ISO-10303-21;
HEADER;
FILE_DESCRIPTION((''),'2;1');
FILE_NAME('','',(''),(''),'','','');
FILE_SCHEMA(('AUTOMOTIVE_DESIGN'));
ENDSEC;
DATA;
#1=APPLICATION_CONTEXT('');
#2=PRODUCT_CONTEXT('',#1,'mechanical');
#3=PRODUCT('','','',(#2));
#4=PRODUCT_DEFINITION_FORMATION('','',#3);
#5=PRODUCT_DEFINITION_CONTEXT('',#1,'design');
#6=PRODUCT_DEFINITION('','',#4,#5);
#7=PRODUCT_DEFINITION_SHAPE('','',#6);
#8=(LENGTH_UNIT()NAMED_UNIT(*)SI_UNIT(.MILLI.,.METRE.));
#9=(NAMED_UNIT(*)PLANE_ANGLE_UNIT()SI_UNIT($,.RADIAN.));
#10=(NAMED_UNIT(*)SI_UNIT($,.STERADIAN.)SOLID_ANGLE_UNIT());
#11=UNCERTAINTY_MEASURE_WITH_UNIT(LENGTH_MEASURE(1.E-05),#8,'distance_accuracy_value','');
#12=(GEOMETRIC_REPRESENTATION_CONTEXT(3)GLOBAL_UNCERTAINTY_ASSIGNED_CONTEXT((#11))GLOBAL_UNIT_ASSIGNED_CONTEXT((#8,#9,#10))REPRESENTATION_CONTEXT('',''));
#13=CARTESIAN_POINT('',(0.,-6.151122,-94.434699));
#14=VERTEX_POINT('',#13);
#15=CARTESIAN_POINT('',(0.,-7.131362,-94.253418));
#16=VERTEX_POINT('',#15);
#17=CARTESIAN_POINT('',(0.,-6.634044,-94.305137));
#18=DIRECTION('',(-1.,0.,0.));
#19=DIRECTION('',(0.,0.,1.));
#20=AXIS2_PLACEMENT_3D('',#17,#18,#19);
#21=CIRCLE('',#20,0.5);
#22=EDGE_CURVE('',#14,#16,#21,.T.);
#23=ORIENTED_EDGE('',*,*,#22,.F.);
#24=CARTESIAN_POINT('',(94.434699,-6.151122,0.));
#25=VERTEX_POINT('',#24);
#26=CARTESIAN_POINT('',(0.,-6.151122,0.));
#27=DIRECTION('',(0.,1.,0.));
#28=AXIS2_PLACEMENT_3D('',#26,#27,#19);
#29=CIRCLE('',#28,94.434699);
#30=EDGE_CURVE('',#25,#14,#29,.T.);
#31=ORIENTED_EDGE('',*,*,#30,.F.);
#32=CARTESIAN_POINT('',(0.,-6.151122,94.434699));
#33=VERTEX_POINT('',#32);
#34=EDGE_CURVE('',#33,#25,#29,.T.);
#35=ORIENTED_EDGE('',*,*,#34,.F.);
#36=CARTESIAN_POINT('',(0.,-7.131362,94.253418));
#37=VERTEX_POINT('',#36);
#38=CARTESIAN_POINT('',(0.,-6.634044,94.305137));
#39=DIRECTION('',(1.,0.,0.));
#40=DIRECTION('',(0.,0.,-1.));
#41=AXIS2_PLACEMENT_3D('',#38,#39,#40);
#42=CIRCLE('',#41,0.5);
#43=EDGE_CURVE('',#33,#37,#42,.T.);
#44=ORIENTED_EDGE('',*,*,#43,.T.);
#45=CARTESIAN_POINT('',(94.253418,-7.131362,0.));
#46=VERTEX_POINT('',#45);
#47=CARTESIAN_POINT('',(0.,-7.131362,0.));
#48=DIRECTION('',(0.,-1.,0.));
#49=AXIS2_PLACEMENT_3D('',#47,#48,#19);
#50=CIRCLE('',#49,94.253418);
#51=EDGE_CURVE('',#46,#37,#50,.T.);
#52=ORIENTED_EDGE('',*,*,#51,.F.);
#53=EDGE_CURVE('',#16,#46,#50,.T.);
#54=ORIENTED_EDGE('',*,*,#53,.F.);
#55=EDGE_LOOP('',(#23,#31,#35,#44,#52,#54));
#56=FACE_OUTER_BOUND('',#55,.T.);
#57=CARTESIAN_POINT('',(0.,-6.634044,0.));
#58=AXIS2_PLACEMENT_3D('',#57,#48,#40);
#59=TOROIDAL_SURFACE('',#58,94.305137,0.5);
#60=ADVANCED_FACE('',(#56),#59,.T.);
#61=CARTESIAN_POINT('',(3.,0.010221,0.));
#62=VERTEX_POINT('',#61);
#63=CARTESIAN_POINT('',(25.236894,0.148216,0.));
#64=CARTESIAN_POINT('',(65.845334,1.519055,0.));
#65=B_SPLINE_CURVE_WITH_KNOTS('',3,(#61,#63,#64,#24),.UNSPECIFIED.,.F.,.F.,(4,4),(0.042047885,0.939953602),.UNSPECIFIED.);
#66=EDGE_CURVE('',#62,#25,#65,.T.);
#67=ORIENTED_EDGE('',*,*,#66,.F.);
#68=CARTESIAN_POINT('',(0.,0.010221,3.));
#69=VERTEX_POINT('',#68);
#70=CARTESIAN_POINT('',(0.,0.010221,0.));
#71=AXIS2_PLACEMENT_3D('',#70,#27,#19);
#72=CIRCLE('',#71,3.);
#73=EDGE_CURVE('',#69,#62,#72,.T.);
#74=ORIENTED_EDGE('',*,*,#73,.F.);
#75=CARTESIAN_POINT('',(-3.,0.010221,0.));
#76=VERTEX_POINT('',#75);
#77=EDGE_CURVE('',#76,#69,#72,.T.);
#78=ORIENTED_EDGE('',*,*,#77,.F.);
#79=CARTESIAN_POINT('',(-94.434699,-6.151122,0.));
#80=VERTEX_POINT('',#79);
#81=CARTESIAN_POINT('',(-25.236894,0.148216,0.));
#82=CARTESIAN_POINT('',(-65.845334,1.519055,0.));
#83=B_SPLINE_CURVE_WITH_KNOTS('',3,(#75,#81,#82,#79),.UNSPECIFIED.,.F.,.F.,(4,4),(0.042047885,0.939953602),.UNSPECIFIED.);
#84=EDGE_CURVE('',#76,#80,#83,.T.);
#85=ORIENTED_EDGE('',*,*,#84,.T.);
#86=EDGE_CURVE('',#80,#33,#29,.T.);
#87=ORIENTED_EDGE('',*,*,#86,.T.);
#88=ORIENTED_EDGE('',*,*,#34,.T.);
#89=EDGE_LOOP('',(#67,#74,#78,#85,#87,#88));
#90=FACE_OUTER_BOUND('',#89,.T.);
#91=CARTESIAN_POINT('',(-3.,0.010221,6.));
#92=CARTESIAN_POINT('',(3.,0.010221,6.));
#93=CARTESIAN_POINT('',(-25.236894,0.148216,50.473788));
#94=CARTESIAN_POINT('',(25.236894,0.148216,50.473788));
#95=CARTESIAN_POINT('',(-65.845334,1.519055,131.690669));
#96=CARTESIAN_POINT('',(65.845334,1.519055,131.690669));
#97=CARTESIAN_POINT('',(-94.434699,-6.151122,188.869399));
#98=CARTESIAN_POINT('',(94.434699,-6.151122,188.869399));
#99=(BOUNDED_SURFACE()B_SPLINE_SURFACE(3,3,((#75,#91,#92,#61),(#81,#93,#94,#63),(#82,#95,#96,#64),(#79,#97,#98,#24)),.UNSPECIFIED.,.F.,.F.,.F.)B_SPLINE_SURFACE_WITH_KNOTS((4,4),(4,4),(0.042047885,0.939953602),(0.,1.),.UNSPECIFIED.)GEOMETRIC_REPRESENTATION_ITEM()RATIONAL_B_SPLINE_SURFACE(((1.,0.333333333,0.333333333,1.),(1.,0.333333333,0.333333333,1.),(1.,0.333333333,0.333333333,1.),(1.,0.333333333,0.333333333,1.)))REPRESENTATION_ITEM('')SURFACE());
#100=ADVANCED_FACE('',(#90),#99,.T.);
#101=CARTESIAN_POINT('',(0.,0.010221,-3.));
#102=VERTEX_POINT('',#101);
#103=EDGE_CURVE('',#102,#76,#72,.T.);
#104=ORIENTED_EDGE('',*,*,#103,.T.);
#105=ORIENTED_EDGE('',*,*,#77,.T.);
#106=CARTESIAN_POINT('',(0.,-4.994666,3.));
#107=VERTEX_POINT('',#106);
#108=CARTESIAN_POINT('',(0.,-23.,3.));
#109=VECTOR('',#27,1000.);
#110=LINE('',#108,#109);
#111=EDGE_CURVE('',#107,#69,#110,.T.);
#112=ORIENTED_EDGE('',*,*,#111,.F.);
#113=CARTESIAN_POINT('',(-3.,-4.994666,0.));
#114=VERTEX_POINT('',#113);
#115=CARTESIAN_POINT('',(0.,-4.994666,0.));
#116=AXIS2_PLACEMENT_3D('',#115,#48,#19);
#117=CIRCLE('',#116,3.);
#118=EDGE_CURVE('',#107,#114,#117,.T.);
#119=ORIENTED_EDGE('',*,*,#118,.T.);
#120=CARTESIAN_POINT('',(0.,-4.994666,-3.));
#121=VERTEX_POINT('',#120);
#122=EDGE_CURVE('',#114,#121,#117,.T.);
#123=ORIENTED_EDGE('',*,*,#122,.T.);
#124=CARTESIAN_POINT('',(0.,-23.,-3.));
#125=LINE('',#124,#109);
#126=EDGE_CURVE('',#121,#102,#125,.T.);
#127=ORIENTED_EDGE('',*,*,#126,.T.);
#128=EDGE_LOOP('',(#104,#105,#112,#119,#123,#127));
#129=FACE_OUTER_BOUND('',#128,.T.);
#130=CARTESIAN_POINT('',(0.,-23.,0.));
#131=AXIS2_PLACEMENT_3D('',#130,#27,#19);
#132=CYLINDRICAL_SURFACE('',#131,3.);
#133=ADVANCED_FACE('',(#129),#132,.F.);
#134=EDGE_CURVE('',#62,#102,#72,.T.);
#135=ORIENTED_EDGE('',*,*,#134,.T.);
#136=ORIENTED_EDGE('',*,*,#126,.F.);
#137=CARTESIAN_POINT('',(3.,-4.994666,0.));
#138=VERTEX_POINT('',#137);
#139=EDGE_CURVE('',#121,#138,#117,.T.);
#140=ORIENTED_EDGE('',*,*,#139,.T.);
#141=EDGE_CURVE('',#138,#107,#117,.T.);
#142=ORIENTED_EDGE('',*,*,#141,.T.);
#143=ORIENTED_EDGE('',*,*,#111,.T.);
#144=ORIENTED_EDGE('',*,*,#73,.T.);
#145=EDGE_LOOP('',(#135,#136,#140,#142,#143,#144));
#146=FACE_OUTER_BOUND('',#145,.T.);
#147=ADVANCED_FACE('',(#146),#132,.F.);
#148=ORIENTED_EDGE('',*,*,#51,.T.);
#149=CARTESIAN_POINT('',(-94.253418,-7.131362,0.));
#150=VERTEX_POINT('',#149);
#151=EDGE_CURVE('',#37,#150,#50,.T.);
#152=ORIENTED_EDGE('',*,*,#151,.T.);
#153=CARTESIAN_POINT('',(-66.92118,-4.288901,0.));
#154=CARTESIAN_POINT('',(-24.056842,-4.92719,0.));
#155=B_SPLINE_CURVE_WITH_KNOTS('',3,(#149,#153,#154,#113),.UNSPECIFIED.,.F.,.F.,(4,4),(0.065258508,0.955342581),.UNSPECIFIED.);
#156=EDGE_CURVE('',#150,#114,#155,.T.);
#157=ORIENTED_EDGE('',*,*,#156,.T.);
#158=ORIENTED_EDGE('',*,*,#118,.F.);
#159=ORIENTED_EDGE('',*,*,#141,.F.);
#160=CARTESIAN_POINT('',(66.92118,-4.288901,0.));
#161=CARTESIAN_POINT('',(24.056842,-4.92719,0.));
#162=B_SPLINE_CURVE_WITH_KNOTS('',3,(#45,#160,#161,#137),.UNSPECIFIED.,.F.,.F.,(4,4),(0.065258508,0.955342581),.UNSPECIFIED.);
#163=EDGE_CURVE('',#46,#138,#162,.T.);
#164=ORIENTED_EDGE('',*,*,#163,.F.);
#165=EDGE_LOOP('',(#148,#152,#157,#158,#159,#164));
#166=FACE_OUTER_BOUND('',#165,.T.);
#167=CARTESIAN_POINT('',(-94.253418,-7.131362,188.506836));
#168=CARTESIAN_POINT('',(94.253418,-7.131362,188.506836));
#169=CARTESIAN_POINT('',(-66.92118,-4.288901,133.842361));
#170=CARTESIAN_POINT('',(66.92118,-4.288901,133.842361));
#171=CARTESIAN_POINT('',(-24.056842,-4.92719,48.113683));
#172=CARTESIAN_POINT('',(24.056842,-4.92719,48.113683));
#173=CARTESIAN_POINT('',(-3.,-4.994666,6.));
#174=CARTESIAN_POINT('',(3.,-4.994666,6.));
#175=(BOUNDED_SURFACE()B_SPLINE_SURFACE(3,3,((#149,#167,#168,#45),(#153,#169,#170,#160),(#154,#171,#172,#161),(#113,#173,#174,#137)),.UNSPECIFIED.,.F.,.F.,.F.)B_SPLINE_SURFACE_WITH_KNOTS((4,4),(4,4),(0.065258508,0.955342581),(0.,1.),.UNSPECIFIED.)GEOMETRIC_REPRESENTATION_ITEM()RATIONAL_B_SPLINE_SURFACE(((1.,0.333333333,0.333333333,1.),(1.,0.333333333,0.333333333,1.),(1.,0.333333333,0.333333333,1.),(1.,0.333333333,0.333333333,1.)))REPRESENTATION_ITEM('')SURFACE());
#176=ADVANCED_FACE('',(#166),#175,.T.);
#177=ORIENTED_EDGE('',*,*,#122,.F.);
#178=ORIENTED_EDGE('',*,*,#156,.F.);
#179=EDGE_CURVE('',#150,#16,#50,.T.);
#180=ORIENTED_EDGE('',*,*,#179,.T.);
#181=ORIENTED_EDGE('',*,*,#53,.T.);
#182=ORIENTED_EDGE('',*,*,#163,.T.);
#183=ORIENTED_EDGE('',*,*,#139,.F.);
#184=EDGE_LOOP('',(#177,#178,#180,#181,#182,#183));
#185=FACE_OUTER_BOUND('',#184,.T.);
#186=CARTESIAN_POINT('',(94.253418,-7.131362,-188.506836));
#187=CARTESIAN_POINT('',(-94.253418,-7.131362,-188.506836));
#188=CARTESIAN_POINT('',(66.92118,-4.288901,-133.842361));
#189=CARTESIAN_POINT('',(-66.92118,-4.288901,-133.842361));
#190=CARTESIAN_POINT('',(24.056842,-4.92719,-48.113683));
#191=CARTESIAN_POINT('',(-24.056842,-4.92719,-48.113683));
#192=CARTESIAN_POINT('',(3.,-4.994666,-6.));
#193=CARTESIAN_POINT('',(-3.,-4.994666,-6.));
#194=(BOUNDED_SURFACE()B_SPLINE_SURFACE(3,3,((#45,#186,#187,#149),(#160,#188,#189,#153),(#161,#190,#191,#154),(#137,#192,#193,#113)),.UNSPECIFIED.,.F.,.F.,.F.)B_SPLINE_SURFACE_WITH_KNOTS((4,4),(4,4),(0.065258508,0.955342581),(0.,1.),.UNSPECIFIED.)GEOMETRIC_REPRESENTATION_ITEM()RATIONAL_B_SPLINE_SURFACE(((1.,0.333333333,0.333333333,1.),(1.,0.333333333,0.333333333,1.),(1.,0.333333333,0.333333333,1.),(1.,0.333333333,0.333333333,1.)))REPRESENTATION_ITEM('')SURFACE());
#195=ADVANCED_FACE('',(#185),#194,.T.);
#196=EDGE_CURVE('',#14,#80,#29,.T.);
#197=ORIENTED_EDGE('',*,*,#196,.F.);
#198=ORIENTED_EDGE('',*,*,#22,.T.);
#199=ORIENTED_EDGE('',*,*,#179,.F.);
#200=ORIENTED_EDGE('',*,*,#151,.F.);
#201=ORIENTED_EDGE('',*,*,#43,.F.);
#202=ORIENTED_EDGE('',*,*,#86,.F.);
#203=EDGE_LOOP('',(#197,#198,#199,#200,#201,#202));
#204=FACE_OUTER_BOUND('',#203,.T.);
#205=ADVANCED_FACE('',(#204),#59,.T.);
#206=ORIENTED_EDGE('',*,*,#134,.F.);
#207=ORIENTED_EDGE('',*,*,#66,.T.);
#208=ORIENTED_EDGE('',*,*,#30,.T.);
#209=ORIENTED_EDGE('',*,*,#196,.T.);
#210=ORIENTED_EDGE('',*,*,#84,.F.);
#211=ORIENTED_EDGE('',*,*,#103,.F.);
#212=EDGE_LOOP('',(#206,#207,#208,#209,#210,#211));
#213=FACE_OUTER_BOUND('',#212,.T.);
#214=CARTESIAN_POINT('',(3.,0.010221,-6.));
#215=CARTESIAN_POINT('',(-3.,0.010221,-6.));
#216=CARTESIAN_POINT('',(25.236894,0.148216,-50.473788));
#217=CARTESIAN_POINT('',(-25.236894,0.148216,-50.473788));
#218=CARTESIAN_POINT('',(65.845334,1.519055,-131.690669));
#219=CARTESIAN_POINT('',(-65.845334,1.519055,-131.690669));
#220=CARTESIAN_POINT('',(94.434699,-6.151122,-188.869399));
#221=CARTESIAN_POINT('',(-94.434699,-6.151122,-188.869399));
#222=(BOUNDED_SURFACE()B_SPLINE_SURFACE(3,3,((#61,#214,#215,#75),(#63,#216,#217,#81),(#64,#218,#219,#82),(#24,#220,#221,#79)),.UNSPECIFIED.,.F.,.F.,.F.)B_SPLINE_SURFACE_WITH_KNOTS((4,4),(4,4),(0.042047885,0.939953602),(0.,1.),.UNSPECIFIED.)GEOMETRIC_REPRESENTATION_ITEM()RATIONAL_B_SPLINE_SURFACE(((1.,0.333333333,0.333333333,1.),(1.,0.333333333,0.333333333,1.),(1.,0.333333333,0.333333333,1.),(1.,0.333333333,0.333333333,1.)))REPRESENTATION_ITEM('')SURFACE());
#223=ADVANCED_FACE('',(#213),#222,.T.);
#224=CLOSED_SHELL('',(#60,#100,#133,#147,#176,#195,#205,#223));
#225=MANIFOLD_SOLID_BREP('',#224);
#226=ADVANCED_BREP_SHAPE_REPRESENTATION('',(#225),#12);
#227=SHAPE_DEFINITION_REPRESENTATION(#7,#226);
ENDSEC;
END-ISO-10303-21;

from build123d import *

# Parameters (mm, degrees)
FILLET_1_R          = 0.5
SKETCH_2_R          = 3
CUT_EXTRUDE_1_DEPTH = 23


with BuildPart() as part:
    # 草图1 → 旋转1 (revolve)
    with BuildSketch(Plane.XY):
        with BuildLine():
            Line((0, 0), (0, -5))
            add(Edge.make_bspline(
                [(-100, -7.814294025), (-72.076817605, -4.022924744), (-21.093053963, -5), (0, -5)],
                knots=[0, 0, 0, 0, 1, 1, 1, 1], degree=3))
            add(Edge.make_bspline(
                [(-100, -7.814294025), (-70.101614167, 2.125878409), (-22.774788705, 0), (0, 0)],
                knots=[0, 0, 0, 0, 1, 1, 1, 1], degree=3))
        make_face()
    revolve(axis=Axis((0, 0, 0), (0, -1, 0)))

    # 圆角1
    fillet_1_edges = [part.edges().sort_by_distance(p)[0] for p in [
        (100, -7.814294025, 0),
    ]]
    fillet(fillet_1_edges, radius=FILLET_1_R)

    # 草图2 → 切除-拉伸1 (cut, symmetric)
    with BuildSketch(Plane(origin=(0, 0, 0), x_dir=(1, 0, 0), z_dir=(0, 1, 0))):
        with Locations(Location((0, 0, 0), (0, 0, 270))):
            Circle(SKETCH_2_R)
    extrude(amount=CUT_EXTRUDE_1_DEPTH, both=True, mode=Mode.SUBTRACT)


solid = part.part
